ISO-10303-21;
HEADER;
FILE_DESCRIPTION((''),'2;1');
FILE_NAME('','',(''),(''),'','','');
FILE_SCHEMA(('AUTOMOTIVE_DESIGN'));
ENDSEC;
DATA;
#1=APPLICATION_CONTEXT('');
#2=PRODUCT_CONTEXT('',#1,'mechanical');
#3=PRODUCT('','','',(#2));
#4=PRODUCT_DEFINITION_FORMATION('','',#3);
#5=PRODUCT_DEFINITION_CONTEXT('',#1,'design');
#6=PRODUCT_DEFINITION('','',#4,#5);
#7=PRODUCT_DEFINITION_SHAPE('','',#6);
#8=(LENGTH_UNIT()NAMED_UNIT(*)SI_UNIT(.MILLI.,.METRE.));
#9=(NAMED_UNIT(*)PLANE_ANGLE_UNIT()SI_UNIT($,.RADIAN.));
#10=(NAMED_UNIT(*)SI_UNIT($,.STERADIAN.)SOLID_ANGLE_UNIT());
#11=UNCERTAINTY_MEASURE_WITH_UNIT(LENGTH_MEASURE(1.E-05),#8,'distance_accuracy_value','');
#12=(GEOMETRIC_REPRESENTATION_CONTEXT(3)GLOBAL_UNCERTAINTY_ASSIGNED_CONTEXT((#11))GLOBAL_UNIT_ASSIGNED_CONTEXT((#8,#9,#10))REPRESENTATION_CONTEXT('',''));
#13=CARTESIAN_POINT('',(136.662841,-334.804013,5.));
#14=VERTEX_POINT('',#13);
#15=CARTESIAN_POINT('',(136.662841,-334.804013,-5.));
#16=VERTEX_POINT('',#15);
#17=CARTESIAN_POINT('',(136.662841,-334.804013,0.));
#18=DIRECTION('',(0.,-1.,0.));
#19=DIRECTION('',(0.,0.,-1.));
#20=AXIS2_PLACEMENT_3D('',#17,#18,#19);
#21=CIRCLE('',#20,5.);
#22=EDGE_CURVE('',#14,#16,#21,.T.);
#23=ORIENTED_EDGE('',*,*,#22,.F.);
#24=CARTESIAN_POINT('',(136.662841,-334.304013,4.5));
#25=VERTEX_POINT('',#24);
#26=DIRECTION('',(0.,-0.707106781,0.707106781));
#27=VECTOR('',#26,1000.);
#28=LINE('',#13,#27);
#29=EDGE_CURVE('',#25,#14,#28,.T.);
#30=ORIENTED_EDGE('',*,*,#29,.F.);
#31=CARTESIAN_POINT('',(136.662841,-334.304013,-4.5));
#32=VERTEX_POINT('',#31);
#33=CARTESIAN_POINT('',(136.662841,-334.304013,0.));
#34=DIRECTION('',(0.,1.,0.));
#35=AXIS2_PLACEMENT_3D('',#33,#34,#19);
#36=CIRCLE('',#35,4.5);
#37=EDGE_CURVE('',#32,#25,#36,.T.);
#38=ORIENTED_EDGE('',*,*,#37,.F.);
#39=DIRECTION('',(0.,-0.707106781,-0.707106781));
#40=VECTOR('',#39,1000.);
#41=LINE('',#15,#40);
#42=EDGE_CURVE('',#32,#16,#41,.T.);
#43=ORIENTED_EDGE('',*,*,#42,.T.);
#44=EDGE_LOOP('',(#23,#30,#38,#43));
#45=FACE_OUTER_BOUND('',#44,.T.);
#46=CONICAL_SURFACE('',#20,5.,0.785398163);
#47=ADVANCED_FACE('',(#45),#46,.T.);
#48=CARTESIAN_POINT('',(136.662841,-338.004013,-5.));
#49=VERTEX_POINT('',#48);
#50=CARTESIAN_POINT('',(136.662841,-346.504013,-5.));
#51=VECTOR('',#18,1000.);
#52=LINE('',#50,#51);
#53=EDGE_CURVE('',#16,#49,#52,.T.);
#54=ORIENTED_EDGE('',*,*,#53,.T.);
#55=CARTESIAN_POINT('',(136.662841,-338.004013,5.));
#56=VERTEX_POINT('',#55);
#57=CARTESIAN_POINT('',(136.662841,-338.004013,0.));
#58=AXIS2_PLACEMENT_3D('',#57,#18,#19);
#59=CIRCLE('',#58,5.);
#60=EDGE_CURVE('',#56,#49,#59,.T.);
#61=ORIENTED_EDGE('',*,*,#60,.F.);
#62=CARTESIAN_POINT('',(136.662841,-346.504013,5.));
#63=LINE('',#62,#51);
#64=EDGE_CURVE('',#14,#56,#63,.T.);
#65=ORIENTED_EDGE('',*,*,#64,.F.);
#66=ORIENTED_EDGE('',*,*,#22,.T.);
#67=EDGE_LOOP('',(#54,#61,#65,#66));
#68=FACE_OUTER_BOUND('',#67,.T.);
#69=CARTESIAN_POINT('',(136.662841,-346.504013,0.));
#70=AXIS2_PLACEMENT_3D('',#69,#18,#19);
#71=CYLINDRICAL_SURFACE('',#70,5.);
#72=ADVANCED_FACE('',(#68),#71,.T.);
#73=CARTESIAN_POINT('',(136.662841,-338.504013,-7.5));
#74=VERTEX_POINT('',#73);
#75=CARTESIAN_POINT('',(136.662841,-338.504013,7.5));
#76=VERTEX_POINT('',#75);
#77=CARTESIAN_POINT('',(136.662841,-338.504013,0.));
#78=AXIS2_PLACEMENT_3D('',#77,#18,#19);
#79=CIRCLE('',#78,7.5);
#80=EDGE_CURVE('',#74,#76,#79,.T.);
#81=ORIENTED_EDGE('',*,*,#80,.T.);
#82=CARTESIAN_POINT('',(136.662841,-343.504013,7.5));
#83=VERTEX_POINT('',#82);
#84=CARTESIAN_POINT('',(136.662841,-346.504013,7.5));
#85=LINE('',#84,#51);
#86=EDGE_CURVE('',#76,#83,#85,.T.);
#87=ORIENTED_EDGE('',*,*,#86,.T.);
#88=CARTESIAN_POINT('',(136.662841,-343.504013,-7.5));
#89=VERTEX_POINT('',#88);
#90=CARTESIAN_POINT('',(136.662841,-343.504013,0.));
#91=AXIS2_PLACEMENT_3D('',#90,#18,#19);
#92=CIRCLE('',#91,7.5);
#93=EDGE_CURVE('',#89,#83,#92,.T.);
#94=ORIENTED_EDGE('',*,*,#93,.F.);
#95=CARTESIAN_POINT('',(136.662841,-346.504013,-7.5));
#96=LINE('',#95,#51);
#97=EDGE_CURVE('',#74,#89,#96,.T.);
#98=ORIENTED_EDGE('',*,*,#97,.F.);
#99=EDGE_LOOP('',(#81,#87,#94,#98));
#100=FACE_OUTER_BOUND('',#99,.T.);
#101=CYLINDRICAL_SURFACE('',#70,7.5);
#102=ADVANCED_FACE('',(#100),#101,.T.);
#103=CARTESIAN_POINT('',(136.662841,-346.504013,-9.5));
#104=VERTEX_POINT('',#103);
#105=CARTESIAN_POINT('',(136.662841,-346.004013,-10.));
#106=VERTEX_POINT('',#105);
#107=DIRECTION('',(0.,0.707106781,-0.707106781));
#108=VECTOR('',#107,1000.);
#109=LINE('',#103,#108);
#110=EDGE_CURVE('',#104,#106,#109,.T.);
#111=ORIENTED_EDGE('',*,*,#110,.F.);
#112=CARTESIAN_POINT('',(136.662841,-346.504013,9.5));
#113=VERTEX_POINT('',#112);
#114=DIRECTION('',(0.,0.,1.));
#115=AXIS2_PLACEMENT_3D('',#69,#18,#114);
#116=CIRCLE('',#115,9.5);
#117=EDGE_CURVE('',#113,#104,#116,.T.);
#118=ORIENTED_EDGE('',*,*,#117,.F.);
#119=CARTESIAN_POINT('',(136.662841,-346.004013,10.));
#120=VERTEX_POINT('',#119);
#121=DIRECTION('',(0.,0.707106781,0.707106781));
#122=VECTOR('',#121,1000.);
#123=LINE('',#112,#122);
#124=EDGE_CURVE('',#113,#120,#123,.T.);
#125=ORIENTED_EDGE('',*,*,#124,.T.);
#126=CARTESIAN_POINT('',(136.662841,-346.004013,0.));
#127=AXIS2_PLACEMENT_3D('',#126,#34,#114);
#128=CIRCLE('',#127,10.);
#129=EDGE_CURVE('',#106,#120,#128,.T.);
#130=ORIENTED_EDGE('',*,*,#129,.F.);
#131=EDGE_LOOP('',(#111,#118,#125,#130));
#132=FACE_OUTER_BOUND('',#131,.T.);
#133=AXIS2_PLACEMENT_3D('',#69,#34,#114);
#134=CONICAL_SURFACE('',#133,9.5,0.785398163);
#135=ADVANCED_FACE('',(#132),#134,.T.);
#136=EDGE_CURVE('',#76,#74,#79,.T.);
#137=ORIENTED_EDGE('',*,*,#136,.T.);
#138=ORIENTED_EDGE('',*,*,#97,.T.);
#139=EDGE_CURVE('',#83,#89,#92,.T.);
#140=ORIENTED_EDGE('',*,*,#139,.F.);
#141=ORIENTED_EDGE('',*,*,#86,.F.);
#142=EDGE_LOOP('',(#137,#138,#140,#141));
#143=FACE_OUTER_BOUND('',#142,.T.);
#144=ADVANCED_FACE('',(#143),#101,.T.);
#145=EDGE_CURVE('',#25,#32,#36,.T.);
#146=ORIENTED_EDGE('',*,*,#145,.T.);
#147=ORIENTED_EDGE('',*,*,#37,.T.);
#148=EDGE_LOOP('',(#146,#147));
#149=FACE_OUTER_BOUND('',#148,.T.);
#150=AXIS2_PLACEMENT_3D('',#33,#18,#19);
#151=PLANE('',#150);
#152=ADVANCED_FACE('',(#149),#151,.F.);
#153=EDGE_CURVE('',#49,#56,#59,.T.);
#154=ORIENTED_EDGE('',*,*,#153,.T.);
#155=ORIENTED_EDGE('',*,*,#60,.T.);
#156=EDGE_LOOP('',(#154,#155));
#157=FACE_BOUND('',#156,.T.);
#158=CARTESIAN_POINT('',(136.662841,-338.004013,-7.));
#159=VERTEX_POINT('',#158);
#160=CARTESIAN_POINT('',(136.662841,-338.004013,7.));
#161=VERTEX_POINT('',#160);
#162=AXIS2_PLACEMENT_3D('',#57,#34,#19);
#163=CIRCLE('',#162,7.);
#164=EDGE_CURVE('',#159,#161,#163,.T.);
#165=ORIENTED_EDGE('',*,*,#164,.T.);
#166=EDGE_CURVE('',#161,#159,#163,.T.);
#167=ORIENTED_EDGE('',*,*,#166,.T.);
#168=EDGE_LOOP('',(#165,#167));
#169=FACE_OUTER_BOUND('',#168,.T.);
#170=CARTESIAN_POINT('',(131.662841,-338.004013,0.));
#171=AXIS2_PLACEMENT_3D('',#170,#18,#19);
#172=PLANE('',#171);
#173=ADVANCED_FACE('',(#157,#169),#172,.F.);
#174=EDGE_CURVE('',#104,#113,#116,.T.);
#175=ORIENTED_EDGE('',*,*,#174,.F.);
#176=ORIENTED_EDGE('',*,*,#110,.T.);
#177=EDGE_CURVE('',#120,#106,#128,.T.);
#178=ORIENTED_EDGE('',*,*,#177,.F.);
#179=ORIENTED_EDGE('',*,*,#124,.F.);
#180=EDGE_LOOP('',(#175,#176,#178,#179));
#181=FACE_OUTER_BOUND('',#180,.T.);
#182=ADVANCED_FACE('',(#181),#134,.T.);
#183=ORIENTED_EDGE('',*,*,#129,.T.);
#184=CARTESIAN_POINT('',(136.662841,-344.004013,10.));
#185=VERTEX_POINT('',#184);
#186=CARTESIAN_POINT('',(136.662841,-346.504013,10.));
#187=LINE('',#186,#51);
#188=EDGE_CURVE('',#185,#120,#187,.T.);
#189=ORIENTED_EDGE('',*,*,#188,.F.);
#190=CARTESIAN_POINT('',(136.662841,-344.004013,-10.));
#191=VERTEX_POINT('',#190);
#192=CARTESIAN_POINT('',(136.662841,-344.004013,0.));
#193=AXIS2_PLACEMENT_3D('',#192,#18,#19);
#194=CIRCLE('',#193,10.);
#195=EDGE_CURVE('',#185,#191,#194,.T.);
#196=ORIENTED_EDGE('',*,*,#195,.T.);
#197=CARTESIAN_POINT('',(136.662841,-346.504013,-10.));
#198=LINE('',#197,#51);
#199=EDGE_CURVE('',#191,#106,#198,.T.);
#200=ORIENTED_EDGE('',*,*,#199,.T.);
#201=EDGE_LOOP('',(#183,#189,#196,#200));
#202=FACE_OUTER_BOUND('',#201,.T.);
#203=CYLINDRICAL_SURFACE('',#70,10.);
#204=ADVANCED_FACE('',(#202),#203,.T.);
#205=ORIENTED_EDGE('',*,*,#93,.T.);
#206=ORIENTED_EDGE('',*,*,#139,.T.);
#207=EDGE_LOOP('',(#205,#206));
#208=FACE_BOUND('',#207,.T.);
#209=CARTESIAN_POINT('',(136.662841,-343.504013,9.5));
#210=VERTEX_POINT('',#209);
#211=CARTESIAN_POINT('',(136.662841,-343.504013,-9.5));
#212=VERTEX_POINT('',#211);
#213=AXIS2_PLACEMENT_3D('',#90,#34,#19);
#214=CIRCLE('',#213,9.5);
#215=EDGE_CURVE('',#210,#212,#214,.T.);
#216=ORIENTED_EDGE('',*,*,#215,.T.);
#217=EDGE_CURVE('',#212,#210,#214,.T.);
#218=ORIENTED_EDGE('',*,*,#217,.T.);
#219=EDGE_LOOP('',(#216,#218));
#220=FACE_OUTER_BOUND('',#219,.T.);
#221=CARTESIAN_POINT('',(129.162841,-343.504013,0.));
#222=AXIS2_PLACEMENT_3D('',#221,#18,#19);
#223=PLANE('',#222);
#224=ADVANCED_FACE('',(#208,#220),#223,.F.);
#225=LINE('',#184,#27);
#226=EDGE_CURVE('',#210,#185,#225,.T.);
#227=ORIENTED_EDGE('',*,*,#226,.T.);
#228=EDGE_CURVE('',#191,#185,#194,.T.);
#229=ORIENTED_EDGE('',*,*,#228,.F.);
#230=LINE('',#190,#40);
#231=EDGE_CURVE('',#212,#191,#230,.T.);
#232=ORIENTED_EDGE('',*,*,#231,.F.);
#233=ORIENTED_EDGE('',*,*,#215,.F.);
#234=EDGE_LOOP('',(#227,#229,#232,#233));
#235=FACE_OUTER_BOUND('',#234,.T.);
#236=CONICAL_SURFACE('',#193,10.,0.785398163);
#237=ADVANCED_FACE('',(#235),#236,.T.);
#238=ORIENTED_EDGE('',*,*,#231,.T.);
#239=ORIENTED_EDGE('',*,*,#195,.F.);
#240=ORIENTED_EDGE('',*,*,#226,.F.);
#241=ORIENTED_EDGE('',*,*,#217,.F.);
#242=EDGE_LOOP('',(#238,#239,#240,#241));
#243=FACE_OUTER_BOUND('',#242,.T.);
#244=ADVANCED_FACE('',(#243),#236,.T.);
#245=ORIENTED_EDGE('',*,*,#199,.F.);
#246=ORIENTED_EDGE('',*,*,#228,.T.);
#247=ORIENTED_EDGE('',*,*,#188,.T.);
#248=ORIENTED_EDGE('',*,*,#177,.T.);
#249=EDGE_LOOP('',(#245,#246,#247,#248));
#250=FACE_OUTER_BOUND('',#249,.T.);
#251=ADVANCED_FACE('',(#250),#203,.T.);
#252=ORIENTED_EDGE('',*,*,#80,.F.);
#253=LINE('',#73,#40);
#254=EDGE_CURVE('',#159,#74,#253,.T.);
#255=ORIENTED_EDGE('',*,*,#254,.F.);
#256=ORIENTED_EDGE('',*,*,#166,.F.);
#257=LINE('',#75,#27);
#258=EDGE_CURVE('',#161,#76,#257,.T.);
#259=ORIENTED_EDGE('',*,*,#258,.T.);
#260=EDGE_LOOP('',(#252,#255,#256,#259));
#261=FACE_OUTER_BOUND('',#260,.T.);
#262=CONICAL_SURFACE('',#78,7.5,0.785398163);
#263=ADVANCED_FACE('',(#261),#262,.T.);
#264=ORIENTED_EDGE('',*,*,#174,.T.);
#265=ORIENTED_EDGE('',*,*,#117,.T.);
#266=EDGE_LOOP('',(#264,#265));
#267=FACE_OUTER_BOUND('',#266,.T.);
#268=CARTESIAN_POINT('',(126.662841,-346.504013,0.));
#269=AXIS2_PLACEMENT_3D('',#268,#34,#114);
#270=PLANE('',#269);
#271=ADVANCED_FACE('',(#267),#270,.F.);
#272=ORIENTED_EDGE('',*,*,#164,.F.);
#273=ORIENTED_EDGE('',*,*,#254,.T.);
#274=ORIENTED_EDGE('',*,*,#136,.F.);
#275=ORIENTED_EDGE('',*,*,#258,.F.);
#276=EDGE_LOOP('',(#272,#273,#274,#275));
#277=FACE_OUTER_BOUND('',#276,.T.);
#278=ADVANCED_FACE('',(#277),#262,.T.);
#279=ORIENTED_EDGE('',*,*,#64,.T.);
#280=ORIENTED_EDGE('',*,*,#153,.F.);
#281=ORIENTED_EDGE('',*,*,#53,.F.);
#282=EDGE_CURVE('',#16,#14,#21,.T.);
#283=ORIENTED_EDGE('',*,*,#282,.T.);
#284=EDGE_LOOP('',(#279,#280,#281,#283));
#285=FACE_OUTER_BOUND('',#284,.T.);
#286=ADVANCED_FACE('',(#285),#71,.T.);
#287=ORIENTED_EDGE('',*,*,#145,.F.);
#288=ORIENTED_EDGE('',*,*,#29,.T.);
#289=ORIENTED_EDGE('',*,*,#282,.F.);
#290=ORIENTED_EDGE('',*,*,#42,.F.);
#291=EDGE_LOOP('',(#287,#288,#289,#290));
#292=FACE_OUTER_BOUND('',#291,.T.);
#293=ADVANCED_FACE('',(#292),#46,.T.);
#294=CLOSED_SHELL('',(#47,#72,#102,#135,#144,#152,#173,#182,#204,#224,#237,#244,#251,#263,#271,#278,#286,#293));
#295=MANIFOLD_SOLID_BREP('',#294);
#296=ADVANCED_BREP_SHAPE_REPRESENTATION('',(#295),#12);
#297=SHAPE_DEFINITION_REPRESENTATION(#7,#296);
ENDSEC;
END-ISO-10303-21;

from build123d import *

# Parameters (mm, degrees)
CHAMFER1_SIZE = 0.5


with BuildPart() as part:
    # Sketch1 → Revolve1 (revolve)
    with BuildSketch(Plane.XY, mode=Mode.PRIVATE) as revolve1_sk:
        Polygon((131.66284067, -334.3040125), (131.66284067, -338.0040125), (129.16284067, -338.0040125), (129.16284067, -343.5040125), (126.66284067, -343.5040125), (126.66284067, -346.5040125), (136.66284067, -346.5040125), (136.66284067, -334.3040125), align=None)
    revolve(revolve1_sk.sketch.rotate(Axis((136.66284067, -346.5040125, 0), (0, 1, 0)), 270), axis=Axis((136.66284067, -346.5040125, 0), (0, 1, 0)))

    # Chamfer1
    chamfer1_edges = [part.edges().sort_by_distance(p)[0] for p in [
        (136.66284067, -334.3040125, 5),
        (136.66284067, -346.5040125, 10),
        (136.66284067, -343.5040125, 10),
        (136.66284067, -338.0040125, 7.5),
    ]]
    chamfer(chamfer1_edges, length=CHAMFER1_SIZE)


solid = part.part
